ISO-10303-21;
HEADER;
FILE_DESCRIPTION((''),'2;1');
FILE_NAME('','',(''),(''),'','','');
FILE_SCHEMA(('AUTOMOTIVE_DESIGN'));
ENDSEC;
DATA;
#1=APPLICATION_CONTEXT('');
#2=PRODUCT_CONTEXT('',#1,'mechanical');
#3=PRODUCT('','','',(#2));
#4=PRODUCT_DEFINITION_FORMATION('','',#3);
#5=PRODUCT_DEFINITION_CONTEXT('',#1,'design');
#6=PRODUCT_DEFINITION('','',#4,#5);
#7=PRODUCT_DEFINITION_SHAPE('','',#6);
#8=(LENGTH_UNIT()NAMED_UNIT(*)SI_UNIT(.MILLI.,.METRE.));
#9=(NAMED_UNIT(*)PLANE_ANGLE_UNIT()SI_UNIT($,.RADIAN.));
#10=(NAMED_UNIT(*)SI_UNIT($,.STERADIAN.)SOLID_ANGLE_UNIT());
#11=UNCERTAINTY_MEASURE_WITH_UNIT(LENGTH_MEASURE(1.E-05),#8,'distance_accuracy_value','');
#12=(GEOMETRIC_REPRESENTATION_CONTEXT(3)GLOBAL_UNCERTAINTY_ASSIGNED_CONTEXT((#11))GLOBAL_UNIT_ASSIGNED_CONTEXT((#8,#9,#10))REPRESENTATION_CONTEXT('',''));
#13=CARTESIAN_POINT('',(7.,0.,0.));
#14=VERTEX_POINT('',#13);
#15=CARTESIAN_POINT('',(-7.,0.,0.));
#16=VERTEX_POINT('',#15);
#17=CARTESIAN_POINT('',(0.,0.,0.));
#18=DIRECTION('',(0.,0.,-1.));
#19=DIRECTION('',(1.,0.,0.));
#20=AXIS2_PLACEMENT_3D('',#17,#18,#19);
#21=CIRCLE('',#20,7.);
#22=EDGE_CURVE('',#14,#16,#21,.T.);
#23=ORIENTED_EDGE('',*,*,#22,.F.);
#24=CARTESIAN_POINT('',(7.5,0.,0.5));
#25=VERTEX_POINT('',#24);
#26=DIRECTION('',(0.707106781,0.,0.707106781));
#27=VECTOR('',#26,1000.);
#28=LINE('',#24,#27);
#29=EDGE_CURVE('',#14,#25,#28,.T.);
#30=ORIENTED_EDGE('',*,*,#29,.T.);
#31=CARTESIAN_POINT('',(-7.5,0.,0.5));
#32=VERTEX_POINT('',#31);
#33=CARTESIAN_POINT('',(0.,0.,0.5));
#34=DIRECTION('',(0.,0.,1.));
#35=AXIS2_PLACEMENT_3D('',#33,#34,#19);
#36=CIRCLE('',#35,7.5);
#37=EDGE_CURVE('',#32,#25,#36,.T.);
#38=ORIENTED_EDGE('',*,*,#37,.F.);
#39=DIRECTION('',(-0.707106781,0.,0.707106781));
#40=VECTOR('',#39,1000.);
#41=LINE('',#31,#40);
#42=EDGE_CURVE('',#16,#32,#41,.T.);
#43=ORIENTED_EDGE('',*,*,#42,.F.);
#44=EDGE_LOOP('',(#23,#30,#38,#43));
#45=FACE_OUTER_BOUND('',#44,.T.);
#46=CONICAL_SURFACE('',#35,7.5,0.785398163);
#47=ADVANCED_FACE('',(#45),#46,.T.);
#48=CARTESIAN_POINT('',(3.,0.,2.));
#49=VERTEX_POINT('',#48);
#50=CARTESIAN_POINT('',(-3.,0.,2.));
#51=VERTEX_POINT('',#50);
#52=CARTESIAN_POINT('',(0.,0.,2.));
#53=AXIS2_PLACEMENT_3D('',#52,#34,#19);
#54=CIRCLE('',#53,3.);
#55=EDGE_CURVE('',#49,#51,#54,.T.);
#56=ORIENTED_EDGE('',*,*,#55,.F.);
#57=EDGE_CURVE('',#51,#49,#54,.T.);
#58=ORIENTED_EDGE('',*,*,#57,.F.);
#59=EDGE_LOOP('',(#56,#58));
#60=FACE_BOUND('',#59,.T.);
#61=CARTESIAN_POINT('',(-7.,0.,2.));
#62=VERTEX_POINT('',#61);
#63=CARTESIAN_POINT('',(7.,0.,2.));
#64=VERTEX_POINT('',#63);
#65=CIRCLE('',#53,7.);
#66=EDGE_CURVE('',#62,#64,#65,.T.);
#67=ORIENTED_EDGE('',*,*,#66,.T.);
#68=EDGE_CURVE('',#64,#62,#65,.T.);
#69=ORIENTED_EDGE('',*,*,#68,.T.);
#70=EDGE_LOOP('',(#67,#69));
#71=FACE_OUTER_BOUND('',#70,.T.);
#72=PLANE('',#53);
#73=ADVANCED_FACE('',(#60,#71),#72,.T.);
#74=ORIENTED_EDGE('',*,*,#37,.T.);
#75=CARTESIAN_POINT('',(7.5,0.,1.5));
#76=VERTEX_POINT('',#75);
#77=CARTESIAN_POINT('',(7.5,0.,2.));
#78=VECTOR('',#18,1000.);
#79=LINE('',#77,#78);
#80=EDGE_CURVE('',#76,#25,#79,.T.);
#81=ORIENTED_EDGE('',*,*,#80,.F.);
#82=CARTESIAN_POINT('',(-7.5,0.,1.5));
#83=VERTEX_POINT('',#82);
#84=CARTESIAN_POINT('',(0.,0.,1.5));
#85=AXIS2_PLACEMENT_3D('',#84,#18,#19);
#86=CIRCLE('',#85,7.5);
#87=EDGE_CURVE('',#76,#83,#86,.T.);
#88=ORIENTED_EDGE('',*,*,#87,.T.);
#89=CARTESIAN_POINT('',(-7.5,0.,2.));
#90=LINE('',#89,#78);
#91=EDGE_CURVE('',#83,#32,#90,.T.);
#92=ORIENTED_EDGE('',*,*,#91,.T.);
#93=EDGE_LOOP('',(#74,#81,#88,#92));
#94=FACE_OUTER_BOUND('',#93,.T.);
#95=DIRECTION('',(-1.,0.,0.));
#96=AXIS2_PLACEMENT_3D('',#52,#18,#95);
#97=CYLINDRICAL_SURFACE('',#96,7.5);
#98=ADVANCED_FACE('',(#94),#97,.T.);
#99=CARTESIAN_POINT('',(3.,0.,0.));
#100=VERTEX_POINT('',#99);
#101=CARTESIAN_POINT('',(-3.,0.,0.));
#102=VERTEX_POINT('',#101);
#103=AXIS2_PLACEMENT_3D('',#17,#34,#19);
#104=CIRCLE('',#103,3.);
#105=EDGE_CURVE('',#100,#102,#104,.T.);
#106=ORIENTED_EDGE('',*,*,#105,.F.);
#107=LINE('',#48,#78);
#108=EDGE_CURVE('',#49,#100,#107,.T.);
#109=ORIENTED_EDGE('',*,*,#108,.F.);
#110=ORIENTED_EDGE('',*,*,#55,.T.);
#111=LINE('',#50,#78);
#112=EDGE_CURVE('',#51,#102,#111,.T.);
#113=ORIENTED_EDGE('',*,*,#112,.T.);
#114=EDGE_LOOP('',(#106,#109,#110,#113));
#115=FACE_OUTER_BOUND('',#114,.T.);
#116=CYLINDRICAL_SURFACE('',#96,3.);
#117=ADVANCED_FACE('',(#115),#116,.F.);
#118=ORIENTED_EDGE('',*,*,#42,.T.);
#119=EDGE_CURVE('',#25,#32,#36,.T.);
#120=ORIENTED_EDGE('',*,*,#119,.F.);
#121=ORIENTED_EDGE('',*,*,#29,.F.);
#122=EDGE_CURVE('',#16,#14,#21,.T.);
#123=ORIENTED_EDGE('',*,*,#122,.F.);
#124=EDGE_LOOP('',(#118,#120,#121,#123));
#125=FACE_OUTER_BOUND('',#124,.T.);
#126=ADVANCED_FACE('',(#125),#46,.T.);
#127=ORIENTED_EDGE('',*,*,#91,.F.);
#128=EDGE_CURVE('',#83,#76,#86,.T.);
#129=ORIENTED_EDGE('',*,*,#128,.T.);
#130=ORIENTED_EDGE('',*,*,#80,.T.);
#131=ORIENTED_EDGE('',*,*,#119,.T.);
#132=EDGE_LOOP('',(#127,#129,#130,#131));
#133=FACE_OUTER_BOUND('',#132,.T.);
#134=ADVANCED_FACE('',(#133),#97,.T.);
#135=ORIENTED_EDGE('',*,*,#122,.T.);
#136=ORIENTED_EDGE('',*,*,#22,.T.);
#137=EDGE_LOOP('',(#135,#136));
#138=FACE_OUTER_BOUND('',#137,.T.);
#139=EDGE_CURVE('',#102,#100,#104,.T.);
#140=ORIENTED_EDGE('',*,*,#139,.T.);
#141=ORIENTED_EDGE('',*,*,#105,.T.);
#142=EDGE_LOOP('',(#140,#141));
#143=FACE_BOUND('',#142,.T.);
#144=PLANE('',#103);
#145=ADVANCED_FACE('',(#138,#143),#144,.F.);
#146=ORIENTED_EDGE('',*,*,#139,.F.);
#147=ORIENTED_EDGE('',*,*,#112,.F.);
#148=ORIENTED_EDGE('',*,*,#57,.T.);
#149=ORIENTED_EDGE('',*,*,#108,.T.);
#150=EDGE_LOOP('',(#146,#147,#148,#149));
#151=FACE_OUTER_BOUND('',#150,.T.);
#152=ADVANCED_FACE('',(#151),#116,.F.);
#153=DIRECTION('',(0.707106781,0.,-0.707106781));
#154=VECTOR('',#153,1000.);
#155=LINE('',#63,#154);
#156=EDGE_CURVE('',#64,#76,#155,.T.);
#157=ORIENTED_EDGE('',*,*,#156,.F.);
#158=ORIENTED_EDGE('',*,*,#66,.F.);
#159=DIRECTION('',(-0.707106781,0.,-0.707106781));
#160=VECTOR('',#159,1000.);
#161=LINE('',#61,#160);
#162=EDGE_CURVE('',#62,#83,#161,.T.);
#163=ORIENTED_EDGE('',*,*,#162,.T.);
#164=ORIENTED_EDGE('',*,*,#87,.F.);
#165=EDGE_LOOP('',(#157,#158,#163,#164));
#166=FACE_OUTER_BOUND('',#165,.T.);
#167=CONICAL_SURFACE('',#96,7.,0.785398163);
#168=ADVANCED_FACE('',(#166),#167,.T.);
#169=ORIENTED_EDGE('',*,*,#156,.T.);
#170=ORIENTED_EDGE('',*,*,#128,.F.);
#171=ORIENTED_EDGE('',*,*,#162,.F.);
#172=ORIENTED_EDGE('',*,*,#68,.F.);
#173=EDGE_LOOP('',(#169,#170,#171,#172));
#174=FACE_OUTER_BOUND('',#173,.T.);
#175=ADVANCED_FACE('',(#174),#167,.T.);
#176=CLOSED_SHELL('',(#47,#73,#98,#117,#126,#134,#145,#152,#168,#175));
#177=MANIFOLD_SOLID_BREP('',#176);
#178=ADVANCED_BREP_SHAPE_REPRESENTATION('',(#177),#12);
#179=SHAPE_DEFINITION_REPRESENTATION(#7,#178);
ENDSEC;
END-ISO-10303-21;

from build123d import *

# Parameters (mm, degrees)
SKETCH1_R           = 7.5
SKETCH1_R_2         = 3
BOSS_EXTRUDE1_DEPTH = 2
CHAMFER1_SIZE       = 0.5


with BuildPart() as part:
    # Sketch1 → Boss-Extrude1 (new body)
    with BuildSketch(Plane.XY):
        Circle(SKETCH1_R)
        Circle(SKETCH1_R_2, mode=Mode.SUBTRACT)
    extrude(amount=BOSS_EXTRUDE1_DEPTH)

    # Chamfer1
    chamfer1_edges = [part.edges().sort_by_distance(p)[0] for p in [
        (-7.5, 0, 0),
        (-7.5, 0, 2),
    ]]
    chamfer(chamfer1_edges, length=CHAMFER1_SIZE)


solid = part.part
